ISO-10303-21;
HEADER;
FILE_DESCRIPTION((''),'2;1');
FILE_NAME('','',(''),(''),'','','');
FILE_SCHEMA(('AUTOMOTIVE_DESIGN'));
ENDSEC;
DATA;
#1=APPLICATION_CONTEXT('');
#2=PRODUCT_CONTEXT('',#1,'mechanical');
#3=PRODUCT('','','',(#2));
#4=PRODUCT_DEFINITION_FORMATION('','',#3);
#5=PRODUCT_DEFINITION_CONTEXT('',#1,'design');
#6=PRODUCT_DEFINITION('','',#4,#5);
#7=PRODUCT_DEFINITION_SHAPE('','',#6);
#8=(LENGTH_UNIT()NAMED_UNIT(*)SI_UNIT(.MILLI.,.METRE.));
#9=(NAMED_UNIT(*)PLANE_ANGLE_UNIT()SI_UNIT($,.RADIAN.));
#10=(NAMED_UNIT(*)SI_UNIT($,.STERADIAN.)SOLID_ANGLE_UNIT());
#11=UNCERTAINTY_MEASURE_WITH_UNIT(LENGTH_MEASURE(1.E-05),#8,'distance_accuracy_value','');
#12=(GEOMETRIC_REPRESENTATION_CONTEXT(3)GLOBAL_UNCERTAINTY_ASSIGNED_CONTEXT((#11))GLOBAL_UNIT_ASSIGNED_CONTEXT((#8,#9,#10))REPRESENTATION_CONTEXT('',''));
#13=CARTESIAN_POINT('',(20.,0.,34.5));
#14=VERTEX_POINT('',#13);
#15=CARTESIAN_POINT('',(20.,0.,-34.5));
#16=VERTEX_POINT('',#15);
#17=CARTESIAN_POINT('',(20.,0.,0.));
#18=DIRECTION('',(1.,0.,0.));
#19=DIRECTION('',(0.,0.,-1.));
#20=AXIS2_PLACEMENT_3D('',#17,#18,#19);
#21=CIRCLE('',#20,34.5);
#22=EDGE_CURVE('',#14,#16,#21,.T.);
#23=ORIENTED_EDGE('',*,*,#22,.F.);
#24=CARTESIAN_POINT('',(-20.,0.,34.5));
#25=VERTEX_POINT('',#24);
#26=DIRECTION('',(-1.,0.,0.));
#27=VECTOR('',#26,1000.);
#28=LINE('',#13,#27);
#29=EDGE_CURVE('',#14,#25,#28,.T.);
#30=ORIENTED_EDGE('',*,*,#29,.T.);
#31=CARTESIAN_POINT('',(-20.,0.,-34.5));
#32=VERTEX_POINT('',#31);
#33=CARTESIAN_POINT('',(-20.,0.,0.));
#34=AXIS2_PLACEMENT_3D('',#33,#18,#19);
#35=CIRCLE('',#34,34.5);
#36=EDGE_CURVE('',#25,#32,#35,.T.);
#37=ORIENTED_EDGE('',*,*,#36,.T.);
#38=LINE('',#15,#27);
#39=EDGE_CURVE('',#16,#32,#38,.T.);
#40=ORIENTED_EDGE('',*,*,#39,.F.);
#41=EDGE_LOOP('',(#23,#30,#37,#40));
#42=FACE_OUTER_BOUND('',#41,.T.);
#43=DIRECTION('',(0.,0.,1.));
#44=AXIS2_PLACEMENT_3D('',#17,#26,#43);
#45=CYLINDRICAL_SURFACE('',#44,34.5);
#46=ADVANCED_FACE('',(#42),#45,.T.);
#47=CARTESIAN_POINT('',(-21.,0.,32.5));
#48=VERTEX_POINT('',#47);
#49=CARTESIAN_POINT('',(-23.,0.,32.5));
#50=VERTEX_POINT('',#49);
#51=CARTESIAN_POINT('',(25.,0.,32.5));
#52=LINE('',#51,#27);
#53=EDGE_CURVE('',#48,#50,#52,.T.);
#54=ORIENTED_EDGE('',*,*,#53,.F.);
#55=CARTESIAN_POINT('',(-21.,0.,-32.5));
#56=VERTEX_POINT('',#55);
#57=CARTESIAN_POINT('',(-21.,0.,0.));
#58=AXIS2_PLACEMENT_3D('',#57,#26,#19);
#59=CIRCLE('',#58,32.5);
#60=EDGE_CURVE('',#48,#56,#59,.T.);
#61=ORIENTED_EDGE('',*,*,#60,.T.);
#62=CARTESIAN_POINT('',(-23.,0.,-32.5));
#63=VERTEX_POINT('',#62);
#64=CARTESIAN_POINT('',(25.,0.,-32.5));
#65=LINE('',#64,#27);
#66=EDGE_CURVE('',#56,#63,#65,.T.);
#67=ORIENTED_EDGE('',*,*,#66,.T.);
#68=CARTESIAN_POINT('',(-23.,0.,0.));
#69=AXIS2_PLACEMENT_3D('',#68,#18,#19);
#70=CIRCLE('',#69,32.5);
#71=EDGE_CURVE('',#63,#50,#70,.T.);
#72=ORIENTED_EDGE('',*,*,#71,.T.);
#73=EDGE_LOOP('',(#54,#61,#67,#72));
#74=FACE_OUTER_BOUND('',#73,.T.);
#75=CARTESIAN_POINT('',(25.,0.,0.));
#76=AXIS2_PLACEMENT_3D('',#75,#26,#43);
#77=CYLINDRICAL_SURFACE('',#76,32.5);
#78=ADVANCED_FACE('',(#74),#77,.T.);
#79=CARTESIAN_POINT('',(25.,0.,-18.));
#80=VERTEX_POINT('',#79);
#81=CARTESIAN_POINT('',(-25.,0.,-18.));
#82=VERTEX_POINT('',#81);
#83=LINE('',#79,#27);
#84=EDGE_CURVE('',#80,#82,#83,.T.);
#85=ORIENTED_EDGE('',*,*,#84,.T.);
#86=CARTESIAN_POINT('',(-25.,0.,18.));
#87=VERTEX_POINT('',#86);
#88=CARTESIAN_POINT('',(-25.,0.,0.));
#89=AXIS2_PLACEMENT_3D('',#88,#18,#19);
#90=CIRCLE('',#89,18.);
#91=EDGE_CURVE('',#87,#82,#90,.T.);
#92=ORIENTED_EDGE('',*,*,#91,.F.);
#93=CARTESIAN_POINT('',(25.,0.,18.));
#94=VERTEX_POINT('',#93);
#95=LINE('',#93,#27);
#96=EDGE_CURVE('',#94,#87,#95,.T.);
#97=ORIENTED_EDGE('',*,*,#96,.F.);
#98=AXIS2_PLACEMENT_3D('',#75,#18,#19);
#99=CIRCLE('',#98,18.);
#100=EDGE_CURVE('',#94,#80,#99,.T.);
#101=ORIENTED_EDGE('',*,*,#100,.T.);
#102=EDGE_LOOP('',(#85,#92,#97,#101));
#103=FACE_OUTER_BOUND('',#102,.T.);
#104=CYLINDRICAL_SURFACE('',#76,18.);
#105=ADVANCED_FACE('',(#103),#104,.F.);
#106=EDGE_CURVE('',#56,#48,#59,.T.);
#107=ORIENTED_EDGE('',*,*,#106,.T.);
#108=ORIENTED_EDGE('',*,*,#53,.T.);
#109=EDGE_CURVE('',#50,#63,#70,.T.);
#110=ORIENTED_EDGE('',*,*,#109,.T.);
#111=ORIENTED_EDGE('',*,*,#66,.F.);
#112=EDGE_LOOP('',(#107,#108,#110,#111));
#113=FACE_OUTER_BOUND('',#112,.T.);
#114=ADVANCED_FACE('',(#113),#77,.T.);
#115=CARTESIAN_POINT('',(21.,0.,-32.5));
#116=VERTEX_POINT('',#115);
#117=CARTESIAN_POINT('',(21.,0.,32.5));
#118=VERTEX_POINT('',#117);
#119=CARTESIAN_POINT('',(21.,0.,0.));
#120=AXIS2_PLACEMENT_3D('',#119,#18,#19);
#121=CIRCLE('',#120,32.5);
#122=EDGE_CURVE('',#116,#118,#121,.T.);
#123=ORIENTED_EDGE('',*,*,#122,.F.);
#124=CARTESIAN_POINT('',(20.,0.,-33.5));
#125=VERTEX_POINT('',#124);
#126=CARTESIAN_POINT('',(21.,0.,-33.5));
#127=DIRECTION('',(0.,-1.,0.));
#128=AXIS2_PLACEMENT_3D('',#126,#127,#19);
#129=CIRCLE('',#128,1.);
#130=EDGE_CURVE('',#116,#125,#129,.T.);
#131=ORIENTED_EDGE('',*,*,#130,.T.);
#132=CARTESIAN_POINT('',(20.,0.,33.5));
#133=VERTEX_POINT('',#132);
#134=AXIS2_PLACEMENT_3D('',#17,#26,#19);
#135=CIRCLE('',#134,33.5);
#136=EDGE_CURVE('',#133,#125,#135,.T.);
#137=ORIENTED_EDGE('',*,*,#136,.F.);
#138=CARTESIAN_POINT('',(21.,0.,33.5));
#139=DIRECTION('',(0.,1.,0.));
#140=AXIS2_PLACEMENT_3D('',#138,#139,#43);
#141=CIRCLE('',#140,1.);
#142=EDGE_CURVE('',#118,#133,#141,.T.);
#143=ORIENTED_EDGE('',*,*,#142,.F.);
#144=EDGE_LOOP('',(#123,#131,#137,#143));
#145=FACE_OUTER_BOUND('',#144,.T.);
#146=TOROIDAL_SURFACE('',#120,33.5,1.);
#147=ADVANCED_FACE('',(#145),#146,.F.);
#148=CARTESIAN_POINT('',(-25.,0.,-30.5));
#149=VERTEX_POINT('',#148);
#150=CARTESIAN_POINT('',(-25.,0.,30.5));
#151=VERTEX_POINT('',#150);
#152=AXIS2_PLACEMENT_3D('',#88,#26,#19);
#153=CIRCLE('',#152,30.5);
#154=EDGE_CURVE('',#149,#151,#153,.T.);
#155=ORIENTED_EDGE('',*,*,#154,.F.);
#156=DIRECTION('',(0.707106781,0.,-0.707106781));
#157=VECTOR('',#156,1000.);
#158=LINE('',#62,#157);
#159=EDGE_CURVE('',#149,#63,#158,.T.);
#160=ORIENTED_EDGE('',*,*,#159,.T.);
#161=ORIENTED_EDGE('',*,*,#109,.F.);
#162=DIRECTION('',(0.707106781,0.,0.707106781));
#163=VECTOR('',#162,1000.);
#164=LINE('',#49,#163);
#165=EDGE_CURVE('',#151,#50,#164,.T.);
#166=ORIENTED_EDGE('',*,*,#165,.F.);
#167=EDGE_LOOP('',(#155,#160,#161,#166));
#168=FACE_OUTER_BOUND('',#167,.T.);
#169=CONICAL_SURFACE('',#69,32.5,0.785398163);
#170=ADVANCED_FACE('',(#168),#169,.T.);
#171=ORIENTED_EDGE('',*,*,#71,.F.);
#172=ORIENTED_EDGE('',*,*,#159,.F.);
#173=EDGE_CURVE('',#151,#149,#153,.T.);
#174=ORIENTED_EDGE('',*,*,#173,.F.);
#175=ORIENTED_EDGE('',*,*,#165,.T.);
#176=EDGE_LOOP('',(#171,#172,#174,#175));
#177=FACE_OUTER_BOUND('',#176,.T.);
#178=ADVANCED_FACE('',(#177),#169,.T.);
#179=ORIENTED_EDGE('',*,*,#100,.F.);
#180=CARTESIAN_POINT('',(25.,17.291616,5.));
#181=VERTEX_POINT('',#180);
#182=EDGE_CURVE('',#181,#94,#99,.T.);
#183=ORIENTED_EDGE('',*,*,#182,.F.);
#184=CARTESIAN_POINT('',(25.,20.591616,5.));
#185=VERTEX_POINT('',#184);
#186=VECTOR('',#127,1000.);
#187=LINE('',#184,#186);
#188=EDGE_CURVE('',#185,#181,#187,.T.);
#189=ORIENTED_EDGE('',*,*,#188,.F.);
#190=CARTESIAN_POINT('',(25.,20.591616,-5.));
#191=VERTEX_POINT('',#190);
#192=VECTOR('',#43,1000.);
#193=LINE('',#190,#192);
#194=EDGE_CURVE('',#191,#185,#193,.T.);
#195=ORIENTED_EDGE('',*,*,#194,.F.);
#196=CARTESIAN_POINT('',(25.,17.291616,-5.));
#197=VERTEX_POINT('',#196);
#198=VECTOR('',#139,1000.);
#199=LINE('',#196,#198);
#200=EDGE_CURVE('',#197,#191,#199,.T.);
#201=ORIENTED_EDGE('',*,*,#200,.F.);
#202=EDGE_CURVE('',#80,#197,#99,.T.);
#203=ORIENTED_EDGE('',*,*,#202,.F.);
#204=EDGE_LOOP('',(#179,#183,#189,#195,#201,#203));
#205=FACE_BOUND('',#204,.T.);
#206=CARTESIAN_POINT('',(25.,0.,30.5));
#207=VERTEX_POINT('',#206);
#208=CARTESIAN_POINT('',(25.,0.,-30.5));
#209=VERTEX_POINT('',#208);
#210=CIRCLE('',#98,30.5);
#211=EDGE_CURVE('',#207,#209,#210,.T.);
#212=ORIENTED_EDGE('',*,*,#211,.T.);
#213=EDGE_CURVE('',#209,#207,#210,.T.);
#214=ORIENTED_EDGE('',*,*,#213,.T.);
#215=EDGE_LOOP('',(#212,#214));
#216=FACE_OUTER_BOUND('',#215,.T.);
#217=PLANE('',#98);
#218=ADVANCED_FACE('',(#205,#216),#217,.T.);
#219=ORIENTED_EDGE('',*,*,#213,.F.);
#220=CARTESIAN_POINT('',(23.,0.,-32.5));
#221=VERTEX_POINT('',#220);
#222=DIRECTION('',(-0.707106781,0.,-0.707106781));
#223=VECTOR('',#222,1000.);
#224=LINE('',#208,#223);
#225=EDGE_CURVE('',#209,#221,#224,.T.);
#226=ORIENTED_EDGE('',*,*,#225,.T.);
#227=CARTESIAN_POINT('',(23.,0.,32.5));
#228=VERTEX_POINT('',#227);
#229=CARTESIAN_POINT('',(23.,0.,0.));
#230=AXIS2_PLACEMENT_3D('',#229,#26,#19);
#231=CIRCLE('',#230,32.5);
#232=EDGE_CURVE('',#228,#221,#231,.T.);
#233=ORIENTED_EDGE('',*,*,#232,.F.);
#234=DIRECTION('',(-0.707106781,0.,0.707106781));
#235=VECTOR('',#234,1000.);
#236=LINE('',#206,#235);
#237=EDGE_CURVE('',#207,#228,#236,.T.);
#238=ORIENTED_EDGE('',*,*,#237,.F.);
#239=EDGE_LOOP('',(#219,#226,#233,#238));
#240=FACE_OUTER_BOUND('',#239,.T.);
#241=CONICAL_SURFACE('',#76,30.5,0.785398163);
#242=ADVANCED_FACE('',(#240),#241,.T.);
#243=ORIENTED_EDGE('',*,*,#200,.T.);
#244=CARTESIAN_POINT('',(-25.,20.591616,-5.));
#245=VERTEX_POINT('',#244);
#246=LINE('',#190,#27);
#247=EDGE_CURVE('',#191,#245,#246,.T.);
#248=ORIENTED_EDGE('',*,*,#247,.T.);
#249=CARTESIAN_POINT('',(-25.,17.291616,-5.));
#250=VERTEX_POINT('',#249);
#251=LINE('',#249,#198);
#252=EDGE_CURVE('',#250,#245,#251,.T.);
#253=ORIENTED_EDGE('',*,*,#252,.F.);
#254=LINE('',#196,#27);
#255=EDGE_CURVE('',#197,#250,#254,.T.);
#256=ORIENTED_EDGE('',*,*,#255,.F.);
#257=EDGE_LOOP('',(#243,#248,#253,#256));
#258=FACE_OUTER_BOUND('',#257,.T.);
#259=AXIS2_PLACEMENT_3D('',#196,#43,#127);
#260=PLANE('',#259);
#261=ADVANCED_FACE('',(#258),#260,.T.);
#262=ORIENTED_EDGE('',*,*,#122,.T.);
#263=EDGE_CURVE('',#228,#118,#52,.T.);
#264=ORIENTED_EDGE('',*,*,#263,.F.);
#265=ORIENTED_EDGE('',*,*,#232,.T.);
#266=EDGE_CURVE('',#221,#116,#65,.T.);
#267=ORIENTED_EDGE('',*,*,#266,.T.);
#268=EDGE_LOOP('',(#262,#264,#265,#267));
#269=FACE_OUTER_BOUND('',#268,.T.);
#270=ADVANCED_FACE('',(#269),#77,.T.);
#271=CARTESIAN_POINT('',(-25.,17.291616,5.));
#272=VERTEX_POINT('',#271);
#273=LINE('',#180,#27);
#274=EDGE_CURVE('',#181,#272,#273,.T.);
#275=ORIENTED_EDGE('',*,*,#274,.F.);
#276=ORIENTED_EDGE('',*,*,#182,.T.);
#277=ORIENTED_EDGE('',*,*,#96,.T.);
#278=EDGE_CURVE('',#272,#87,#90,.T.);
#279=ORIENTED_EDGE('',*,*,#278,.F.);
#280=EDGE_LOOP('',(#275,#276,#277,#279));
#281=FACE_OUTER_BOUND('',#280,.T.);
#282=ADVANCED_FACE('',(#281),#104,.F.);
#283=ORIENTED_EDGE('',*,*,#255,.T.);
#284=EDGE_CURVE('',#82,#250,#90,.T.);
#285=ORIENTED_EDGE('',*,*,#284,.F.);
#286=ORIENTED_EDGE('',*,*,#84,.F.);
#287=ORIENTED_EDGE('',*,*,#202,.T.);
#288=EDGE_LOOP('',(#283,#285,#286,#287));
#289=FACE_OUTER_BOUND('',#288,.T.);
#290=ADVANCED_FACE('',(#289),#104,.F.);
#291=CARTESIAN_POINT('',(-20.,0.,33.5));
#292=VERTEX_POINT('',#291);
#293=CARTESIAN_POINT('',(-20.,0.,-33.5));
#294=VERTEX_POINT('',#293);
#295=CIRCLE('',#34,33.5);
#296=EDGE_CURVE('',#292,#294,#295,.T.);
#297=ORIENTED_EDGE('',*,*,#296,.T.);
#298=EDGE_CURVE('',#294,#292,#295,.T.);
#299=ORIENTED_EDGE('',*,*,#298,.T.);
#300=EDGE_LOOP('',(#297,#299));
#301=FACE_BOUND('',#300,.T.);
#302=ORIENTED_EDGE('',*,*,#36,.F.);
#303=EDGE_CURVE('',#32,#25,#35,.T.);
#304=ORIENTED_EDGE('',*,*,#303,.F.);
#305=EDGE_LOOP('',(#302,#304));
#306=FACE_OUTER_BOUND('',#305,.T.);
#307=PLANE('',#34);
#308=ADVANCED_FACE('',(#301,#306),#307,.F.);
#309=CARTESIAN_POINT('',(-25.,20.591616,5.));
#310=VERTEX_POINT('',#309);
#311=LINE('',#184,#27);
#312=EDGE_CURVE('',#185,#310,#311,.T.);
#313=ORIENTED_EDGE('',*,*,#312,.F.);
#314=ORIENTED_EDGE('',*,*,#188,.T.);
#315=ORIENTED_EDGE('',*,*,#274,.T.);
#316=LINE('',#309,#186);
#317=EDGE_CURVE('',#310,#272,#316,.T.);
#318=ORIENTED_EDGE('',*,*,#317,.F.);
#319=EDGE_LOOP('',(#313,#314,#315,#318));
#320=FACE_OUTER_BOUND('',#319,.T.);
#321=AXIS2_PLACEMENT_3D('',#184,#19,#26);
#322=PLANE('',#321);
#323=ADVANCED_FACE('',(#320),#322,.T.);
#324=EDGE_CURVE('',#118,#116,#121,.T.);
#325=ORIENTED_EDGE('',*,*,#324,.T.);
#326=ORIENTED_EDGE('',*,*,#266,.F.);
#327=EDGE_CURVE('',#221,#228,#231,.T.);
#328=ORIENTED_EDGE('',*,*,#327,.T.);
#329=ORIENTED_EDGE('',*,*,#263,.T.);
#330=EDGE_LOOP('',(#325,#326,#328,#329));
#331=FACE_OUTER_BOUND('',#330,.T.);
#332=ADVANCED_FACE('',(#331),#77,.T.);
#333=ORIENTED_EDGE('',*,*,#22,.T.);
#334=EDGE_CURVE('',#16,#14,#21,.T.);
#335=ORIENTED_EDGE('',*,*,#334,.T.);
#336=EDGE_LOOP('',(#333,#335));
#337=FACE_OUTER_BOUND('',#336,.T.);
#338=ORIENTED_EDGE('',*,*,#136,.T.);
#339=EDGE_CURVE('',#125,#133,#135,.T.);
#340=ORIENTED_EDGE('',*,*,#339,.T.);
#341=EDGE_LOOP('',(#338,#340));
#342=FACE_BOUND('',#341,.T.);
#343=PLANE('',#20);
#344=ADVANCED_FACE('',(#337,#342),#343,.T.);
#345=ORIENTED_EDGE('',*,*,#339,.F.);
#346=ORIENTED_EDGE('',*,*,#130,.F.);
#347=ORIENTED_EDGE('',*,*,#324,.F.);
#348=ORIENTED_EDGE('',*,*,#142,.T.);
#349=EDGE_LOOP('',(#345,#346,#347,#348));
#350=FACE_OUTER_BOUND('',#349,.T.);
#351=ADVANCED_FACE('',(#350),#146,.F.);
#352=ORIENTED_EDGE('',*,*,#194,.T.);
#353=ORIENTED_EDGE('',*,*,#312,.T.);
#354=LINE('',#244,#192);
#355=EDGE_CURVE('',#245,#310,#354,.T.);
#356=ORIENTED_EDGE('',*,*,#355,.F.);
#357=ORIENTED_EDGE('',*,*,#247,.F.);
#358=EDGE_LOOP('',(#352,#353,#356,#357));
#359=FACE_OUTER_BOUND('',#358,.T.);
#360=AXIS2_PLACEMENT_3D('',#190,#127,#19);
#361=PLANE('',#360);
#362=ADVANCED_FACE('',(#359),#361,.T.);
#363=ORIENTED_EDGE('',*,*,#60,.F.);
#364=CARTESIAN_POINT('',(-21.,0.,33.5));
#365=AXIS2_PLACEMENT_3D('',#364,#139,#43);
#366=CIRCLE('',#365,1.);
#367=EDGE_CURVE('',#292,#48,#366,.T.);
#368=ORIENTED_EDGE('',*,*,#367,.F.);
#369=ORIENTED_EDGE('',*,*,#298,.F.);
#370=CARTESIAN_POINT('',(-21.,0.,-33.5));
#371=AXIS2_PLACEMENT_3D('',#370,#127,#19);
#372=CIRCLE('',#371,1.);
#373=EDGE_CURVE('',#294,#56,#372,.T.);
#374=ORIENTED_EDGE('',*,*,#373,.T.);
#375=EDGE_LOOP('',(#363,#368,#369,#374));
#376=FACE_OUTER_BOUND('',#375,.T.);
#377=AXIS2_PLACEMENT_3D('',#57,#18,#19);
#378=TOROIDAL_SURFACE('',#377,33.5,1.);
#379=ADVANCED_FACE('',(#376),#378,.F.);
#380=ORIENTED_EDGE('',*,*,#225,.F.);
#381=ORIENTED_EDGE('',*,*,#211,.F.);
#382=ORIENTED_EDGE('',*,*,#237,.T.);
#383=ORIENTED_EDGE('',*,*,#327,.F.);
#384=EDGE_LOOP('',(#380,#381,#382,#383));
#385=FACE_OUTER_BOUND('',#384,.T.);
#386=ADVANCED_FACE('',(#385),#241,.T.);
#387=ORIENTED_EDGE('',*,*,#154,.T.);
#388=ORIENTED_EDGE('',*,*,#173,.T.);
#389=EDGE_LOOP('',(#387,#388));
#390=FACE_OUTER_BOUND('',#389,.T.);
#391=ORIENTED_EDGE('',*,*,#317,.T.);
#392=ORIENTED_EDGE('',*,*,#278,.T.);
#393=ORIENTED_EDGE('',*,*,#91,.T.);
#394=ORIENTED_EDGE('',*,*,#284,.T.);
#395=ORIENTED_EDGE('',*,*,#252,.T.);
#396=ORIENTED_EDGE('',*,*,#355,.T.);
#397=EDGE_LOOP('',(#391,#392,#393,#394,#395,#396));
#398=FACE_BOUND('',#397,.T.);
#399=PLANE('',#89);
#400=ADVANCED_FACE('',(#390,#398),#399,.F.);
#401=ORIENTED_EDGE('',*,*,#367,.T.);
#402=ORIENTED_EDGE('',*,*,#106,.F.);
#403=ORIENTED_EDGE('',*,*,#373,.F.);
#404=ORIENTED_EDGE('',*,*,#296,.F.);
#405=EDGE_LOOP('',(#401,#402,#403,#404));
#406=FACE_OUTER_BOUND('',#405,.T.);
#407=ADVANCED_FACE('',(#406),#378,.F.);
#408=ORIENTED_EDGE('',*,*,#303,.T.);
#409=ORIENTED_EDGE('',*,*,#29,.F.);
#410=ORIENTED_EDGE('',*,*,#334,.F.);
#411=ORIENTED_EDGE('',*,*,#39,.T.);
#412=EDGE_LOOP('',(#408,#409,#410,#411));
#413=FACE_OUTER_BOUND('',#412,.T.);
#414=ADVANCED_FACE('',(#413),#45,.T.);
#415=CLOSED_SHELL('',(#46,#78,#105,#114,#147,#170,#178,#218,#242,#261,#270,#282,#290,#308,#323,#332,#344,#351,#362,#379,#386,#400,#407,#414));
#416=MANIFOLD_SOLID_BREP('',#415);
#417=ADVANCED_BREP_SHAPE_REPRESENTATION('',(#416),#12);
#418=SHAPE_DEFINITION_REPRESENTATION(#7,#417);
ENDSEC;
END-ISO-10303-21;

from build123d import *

# Parameters (mm, degrees)
SKETCH_1_R      = 32.5
EXTRUDE_1_DEPTH = 25
SKETCH_2_R      = 34.5
SKETCH_2_R_2    = 32.5
EXTRUDE_2_DEPTH = 20
FILLET_1_R      = 1
CHAMFER_1_SIZE  = 2


with BuildPart() as part:
    # 草图1 → 凸台-拉伸1 (new, symmetric)
    with BuildSketch(Plane(origin=(0, 0, 0), x_dir=(0, 0, -1), z_dir=(1, 0, 0))):
        Circle(SKETCH_1_R)
        with BuildLine():
            Line((5, 17.291616466), (5, 20.591616466))
            Line((5, 20.591616466), (-5, 20.591616466))
            Line((-5, 20.591616466), (-5, 17.291616466))
            ThreePointArc((-5, 17.291616466), (0, -18), (5, 17.291616466))
        make_face(mode=Mode.SUBTRACT)
    extrude(amount=EXTRUDE_1_DEPTH, both=True)

    # 草图2 → 凸台-拉伸2 (add, symmetric)
    with BuildSketch(Plane(origin=(0, 0, 0), x_dir=(0, 0, -1), z_dir=(1, 0, 0))):
        Circle(SKETCH_2_R)
        Circle(SKETCH_2_R_2, mode=Mode.SUBTRACT)
    extrude(amount=EXTRUDE_2_DEPTH, both=True)

    # 圆角1
    fillet_1_edges = [part.edges().sort_by_distance(p)[0] for p in [
        (-20, 0, 32.5),
        (20, 0, 32.5),
    ]]
    fillet(fillet_1_edges, radius=FILLET_1_R)

    # 倒角1
    chamfer_1_edges = [part.edges().sort_by_distance(p)[0] for p in [
        (-25, 0, 32.5),
        (25, 0, 32.5),
    ]]
    chamfer(chamfer_1_edges, length=CHAMFER_1_SIZE)


solid = part.part
